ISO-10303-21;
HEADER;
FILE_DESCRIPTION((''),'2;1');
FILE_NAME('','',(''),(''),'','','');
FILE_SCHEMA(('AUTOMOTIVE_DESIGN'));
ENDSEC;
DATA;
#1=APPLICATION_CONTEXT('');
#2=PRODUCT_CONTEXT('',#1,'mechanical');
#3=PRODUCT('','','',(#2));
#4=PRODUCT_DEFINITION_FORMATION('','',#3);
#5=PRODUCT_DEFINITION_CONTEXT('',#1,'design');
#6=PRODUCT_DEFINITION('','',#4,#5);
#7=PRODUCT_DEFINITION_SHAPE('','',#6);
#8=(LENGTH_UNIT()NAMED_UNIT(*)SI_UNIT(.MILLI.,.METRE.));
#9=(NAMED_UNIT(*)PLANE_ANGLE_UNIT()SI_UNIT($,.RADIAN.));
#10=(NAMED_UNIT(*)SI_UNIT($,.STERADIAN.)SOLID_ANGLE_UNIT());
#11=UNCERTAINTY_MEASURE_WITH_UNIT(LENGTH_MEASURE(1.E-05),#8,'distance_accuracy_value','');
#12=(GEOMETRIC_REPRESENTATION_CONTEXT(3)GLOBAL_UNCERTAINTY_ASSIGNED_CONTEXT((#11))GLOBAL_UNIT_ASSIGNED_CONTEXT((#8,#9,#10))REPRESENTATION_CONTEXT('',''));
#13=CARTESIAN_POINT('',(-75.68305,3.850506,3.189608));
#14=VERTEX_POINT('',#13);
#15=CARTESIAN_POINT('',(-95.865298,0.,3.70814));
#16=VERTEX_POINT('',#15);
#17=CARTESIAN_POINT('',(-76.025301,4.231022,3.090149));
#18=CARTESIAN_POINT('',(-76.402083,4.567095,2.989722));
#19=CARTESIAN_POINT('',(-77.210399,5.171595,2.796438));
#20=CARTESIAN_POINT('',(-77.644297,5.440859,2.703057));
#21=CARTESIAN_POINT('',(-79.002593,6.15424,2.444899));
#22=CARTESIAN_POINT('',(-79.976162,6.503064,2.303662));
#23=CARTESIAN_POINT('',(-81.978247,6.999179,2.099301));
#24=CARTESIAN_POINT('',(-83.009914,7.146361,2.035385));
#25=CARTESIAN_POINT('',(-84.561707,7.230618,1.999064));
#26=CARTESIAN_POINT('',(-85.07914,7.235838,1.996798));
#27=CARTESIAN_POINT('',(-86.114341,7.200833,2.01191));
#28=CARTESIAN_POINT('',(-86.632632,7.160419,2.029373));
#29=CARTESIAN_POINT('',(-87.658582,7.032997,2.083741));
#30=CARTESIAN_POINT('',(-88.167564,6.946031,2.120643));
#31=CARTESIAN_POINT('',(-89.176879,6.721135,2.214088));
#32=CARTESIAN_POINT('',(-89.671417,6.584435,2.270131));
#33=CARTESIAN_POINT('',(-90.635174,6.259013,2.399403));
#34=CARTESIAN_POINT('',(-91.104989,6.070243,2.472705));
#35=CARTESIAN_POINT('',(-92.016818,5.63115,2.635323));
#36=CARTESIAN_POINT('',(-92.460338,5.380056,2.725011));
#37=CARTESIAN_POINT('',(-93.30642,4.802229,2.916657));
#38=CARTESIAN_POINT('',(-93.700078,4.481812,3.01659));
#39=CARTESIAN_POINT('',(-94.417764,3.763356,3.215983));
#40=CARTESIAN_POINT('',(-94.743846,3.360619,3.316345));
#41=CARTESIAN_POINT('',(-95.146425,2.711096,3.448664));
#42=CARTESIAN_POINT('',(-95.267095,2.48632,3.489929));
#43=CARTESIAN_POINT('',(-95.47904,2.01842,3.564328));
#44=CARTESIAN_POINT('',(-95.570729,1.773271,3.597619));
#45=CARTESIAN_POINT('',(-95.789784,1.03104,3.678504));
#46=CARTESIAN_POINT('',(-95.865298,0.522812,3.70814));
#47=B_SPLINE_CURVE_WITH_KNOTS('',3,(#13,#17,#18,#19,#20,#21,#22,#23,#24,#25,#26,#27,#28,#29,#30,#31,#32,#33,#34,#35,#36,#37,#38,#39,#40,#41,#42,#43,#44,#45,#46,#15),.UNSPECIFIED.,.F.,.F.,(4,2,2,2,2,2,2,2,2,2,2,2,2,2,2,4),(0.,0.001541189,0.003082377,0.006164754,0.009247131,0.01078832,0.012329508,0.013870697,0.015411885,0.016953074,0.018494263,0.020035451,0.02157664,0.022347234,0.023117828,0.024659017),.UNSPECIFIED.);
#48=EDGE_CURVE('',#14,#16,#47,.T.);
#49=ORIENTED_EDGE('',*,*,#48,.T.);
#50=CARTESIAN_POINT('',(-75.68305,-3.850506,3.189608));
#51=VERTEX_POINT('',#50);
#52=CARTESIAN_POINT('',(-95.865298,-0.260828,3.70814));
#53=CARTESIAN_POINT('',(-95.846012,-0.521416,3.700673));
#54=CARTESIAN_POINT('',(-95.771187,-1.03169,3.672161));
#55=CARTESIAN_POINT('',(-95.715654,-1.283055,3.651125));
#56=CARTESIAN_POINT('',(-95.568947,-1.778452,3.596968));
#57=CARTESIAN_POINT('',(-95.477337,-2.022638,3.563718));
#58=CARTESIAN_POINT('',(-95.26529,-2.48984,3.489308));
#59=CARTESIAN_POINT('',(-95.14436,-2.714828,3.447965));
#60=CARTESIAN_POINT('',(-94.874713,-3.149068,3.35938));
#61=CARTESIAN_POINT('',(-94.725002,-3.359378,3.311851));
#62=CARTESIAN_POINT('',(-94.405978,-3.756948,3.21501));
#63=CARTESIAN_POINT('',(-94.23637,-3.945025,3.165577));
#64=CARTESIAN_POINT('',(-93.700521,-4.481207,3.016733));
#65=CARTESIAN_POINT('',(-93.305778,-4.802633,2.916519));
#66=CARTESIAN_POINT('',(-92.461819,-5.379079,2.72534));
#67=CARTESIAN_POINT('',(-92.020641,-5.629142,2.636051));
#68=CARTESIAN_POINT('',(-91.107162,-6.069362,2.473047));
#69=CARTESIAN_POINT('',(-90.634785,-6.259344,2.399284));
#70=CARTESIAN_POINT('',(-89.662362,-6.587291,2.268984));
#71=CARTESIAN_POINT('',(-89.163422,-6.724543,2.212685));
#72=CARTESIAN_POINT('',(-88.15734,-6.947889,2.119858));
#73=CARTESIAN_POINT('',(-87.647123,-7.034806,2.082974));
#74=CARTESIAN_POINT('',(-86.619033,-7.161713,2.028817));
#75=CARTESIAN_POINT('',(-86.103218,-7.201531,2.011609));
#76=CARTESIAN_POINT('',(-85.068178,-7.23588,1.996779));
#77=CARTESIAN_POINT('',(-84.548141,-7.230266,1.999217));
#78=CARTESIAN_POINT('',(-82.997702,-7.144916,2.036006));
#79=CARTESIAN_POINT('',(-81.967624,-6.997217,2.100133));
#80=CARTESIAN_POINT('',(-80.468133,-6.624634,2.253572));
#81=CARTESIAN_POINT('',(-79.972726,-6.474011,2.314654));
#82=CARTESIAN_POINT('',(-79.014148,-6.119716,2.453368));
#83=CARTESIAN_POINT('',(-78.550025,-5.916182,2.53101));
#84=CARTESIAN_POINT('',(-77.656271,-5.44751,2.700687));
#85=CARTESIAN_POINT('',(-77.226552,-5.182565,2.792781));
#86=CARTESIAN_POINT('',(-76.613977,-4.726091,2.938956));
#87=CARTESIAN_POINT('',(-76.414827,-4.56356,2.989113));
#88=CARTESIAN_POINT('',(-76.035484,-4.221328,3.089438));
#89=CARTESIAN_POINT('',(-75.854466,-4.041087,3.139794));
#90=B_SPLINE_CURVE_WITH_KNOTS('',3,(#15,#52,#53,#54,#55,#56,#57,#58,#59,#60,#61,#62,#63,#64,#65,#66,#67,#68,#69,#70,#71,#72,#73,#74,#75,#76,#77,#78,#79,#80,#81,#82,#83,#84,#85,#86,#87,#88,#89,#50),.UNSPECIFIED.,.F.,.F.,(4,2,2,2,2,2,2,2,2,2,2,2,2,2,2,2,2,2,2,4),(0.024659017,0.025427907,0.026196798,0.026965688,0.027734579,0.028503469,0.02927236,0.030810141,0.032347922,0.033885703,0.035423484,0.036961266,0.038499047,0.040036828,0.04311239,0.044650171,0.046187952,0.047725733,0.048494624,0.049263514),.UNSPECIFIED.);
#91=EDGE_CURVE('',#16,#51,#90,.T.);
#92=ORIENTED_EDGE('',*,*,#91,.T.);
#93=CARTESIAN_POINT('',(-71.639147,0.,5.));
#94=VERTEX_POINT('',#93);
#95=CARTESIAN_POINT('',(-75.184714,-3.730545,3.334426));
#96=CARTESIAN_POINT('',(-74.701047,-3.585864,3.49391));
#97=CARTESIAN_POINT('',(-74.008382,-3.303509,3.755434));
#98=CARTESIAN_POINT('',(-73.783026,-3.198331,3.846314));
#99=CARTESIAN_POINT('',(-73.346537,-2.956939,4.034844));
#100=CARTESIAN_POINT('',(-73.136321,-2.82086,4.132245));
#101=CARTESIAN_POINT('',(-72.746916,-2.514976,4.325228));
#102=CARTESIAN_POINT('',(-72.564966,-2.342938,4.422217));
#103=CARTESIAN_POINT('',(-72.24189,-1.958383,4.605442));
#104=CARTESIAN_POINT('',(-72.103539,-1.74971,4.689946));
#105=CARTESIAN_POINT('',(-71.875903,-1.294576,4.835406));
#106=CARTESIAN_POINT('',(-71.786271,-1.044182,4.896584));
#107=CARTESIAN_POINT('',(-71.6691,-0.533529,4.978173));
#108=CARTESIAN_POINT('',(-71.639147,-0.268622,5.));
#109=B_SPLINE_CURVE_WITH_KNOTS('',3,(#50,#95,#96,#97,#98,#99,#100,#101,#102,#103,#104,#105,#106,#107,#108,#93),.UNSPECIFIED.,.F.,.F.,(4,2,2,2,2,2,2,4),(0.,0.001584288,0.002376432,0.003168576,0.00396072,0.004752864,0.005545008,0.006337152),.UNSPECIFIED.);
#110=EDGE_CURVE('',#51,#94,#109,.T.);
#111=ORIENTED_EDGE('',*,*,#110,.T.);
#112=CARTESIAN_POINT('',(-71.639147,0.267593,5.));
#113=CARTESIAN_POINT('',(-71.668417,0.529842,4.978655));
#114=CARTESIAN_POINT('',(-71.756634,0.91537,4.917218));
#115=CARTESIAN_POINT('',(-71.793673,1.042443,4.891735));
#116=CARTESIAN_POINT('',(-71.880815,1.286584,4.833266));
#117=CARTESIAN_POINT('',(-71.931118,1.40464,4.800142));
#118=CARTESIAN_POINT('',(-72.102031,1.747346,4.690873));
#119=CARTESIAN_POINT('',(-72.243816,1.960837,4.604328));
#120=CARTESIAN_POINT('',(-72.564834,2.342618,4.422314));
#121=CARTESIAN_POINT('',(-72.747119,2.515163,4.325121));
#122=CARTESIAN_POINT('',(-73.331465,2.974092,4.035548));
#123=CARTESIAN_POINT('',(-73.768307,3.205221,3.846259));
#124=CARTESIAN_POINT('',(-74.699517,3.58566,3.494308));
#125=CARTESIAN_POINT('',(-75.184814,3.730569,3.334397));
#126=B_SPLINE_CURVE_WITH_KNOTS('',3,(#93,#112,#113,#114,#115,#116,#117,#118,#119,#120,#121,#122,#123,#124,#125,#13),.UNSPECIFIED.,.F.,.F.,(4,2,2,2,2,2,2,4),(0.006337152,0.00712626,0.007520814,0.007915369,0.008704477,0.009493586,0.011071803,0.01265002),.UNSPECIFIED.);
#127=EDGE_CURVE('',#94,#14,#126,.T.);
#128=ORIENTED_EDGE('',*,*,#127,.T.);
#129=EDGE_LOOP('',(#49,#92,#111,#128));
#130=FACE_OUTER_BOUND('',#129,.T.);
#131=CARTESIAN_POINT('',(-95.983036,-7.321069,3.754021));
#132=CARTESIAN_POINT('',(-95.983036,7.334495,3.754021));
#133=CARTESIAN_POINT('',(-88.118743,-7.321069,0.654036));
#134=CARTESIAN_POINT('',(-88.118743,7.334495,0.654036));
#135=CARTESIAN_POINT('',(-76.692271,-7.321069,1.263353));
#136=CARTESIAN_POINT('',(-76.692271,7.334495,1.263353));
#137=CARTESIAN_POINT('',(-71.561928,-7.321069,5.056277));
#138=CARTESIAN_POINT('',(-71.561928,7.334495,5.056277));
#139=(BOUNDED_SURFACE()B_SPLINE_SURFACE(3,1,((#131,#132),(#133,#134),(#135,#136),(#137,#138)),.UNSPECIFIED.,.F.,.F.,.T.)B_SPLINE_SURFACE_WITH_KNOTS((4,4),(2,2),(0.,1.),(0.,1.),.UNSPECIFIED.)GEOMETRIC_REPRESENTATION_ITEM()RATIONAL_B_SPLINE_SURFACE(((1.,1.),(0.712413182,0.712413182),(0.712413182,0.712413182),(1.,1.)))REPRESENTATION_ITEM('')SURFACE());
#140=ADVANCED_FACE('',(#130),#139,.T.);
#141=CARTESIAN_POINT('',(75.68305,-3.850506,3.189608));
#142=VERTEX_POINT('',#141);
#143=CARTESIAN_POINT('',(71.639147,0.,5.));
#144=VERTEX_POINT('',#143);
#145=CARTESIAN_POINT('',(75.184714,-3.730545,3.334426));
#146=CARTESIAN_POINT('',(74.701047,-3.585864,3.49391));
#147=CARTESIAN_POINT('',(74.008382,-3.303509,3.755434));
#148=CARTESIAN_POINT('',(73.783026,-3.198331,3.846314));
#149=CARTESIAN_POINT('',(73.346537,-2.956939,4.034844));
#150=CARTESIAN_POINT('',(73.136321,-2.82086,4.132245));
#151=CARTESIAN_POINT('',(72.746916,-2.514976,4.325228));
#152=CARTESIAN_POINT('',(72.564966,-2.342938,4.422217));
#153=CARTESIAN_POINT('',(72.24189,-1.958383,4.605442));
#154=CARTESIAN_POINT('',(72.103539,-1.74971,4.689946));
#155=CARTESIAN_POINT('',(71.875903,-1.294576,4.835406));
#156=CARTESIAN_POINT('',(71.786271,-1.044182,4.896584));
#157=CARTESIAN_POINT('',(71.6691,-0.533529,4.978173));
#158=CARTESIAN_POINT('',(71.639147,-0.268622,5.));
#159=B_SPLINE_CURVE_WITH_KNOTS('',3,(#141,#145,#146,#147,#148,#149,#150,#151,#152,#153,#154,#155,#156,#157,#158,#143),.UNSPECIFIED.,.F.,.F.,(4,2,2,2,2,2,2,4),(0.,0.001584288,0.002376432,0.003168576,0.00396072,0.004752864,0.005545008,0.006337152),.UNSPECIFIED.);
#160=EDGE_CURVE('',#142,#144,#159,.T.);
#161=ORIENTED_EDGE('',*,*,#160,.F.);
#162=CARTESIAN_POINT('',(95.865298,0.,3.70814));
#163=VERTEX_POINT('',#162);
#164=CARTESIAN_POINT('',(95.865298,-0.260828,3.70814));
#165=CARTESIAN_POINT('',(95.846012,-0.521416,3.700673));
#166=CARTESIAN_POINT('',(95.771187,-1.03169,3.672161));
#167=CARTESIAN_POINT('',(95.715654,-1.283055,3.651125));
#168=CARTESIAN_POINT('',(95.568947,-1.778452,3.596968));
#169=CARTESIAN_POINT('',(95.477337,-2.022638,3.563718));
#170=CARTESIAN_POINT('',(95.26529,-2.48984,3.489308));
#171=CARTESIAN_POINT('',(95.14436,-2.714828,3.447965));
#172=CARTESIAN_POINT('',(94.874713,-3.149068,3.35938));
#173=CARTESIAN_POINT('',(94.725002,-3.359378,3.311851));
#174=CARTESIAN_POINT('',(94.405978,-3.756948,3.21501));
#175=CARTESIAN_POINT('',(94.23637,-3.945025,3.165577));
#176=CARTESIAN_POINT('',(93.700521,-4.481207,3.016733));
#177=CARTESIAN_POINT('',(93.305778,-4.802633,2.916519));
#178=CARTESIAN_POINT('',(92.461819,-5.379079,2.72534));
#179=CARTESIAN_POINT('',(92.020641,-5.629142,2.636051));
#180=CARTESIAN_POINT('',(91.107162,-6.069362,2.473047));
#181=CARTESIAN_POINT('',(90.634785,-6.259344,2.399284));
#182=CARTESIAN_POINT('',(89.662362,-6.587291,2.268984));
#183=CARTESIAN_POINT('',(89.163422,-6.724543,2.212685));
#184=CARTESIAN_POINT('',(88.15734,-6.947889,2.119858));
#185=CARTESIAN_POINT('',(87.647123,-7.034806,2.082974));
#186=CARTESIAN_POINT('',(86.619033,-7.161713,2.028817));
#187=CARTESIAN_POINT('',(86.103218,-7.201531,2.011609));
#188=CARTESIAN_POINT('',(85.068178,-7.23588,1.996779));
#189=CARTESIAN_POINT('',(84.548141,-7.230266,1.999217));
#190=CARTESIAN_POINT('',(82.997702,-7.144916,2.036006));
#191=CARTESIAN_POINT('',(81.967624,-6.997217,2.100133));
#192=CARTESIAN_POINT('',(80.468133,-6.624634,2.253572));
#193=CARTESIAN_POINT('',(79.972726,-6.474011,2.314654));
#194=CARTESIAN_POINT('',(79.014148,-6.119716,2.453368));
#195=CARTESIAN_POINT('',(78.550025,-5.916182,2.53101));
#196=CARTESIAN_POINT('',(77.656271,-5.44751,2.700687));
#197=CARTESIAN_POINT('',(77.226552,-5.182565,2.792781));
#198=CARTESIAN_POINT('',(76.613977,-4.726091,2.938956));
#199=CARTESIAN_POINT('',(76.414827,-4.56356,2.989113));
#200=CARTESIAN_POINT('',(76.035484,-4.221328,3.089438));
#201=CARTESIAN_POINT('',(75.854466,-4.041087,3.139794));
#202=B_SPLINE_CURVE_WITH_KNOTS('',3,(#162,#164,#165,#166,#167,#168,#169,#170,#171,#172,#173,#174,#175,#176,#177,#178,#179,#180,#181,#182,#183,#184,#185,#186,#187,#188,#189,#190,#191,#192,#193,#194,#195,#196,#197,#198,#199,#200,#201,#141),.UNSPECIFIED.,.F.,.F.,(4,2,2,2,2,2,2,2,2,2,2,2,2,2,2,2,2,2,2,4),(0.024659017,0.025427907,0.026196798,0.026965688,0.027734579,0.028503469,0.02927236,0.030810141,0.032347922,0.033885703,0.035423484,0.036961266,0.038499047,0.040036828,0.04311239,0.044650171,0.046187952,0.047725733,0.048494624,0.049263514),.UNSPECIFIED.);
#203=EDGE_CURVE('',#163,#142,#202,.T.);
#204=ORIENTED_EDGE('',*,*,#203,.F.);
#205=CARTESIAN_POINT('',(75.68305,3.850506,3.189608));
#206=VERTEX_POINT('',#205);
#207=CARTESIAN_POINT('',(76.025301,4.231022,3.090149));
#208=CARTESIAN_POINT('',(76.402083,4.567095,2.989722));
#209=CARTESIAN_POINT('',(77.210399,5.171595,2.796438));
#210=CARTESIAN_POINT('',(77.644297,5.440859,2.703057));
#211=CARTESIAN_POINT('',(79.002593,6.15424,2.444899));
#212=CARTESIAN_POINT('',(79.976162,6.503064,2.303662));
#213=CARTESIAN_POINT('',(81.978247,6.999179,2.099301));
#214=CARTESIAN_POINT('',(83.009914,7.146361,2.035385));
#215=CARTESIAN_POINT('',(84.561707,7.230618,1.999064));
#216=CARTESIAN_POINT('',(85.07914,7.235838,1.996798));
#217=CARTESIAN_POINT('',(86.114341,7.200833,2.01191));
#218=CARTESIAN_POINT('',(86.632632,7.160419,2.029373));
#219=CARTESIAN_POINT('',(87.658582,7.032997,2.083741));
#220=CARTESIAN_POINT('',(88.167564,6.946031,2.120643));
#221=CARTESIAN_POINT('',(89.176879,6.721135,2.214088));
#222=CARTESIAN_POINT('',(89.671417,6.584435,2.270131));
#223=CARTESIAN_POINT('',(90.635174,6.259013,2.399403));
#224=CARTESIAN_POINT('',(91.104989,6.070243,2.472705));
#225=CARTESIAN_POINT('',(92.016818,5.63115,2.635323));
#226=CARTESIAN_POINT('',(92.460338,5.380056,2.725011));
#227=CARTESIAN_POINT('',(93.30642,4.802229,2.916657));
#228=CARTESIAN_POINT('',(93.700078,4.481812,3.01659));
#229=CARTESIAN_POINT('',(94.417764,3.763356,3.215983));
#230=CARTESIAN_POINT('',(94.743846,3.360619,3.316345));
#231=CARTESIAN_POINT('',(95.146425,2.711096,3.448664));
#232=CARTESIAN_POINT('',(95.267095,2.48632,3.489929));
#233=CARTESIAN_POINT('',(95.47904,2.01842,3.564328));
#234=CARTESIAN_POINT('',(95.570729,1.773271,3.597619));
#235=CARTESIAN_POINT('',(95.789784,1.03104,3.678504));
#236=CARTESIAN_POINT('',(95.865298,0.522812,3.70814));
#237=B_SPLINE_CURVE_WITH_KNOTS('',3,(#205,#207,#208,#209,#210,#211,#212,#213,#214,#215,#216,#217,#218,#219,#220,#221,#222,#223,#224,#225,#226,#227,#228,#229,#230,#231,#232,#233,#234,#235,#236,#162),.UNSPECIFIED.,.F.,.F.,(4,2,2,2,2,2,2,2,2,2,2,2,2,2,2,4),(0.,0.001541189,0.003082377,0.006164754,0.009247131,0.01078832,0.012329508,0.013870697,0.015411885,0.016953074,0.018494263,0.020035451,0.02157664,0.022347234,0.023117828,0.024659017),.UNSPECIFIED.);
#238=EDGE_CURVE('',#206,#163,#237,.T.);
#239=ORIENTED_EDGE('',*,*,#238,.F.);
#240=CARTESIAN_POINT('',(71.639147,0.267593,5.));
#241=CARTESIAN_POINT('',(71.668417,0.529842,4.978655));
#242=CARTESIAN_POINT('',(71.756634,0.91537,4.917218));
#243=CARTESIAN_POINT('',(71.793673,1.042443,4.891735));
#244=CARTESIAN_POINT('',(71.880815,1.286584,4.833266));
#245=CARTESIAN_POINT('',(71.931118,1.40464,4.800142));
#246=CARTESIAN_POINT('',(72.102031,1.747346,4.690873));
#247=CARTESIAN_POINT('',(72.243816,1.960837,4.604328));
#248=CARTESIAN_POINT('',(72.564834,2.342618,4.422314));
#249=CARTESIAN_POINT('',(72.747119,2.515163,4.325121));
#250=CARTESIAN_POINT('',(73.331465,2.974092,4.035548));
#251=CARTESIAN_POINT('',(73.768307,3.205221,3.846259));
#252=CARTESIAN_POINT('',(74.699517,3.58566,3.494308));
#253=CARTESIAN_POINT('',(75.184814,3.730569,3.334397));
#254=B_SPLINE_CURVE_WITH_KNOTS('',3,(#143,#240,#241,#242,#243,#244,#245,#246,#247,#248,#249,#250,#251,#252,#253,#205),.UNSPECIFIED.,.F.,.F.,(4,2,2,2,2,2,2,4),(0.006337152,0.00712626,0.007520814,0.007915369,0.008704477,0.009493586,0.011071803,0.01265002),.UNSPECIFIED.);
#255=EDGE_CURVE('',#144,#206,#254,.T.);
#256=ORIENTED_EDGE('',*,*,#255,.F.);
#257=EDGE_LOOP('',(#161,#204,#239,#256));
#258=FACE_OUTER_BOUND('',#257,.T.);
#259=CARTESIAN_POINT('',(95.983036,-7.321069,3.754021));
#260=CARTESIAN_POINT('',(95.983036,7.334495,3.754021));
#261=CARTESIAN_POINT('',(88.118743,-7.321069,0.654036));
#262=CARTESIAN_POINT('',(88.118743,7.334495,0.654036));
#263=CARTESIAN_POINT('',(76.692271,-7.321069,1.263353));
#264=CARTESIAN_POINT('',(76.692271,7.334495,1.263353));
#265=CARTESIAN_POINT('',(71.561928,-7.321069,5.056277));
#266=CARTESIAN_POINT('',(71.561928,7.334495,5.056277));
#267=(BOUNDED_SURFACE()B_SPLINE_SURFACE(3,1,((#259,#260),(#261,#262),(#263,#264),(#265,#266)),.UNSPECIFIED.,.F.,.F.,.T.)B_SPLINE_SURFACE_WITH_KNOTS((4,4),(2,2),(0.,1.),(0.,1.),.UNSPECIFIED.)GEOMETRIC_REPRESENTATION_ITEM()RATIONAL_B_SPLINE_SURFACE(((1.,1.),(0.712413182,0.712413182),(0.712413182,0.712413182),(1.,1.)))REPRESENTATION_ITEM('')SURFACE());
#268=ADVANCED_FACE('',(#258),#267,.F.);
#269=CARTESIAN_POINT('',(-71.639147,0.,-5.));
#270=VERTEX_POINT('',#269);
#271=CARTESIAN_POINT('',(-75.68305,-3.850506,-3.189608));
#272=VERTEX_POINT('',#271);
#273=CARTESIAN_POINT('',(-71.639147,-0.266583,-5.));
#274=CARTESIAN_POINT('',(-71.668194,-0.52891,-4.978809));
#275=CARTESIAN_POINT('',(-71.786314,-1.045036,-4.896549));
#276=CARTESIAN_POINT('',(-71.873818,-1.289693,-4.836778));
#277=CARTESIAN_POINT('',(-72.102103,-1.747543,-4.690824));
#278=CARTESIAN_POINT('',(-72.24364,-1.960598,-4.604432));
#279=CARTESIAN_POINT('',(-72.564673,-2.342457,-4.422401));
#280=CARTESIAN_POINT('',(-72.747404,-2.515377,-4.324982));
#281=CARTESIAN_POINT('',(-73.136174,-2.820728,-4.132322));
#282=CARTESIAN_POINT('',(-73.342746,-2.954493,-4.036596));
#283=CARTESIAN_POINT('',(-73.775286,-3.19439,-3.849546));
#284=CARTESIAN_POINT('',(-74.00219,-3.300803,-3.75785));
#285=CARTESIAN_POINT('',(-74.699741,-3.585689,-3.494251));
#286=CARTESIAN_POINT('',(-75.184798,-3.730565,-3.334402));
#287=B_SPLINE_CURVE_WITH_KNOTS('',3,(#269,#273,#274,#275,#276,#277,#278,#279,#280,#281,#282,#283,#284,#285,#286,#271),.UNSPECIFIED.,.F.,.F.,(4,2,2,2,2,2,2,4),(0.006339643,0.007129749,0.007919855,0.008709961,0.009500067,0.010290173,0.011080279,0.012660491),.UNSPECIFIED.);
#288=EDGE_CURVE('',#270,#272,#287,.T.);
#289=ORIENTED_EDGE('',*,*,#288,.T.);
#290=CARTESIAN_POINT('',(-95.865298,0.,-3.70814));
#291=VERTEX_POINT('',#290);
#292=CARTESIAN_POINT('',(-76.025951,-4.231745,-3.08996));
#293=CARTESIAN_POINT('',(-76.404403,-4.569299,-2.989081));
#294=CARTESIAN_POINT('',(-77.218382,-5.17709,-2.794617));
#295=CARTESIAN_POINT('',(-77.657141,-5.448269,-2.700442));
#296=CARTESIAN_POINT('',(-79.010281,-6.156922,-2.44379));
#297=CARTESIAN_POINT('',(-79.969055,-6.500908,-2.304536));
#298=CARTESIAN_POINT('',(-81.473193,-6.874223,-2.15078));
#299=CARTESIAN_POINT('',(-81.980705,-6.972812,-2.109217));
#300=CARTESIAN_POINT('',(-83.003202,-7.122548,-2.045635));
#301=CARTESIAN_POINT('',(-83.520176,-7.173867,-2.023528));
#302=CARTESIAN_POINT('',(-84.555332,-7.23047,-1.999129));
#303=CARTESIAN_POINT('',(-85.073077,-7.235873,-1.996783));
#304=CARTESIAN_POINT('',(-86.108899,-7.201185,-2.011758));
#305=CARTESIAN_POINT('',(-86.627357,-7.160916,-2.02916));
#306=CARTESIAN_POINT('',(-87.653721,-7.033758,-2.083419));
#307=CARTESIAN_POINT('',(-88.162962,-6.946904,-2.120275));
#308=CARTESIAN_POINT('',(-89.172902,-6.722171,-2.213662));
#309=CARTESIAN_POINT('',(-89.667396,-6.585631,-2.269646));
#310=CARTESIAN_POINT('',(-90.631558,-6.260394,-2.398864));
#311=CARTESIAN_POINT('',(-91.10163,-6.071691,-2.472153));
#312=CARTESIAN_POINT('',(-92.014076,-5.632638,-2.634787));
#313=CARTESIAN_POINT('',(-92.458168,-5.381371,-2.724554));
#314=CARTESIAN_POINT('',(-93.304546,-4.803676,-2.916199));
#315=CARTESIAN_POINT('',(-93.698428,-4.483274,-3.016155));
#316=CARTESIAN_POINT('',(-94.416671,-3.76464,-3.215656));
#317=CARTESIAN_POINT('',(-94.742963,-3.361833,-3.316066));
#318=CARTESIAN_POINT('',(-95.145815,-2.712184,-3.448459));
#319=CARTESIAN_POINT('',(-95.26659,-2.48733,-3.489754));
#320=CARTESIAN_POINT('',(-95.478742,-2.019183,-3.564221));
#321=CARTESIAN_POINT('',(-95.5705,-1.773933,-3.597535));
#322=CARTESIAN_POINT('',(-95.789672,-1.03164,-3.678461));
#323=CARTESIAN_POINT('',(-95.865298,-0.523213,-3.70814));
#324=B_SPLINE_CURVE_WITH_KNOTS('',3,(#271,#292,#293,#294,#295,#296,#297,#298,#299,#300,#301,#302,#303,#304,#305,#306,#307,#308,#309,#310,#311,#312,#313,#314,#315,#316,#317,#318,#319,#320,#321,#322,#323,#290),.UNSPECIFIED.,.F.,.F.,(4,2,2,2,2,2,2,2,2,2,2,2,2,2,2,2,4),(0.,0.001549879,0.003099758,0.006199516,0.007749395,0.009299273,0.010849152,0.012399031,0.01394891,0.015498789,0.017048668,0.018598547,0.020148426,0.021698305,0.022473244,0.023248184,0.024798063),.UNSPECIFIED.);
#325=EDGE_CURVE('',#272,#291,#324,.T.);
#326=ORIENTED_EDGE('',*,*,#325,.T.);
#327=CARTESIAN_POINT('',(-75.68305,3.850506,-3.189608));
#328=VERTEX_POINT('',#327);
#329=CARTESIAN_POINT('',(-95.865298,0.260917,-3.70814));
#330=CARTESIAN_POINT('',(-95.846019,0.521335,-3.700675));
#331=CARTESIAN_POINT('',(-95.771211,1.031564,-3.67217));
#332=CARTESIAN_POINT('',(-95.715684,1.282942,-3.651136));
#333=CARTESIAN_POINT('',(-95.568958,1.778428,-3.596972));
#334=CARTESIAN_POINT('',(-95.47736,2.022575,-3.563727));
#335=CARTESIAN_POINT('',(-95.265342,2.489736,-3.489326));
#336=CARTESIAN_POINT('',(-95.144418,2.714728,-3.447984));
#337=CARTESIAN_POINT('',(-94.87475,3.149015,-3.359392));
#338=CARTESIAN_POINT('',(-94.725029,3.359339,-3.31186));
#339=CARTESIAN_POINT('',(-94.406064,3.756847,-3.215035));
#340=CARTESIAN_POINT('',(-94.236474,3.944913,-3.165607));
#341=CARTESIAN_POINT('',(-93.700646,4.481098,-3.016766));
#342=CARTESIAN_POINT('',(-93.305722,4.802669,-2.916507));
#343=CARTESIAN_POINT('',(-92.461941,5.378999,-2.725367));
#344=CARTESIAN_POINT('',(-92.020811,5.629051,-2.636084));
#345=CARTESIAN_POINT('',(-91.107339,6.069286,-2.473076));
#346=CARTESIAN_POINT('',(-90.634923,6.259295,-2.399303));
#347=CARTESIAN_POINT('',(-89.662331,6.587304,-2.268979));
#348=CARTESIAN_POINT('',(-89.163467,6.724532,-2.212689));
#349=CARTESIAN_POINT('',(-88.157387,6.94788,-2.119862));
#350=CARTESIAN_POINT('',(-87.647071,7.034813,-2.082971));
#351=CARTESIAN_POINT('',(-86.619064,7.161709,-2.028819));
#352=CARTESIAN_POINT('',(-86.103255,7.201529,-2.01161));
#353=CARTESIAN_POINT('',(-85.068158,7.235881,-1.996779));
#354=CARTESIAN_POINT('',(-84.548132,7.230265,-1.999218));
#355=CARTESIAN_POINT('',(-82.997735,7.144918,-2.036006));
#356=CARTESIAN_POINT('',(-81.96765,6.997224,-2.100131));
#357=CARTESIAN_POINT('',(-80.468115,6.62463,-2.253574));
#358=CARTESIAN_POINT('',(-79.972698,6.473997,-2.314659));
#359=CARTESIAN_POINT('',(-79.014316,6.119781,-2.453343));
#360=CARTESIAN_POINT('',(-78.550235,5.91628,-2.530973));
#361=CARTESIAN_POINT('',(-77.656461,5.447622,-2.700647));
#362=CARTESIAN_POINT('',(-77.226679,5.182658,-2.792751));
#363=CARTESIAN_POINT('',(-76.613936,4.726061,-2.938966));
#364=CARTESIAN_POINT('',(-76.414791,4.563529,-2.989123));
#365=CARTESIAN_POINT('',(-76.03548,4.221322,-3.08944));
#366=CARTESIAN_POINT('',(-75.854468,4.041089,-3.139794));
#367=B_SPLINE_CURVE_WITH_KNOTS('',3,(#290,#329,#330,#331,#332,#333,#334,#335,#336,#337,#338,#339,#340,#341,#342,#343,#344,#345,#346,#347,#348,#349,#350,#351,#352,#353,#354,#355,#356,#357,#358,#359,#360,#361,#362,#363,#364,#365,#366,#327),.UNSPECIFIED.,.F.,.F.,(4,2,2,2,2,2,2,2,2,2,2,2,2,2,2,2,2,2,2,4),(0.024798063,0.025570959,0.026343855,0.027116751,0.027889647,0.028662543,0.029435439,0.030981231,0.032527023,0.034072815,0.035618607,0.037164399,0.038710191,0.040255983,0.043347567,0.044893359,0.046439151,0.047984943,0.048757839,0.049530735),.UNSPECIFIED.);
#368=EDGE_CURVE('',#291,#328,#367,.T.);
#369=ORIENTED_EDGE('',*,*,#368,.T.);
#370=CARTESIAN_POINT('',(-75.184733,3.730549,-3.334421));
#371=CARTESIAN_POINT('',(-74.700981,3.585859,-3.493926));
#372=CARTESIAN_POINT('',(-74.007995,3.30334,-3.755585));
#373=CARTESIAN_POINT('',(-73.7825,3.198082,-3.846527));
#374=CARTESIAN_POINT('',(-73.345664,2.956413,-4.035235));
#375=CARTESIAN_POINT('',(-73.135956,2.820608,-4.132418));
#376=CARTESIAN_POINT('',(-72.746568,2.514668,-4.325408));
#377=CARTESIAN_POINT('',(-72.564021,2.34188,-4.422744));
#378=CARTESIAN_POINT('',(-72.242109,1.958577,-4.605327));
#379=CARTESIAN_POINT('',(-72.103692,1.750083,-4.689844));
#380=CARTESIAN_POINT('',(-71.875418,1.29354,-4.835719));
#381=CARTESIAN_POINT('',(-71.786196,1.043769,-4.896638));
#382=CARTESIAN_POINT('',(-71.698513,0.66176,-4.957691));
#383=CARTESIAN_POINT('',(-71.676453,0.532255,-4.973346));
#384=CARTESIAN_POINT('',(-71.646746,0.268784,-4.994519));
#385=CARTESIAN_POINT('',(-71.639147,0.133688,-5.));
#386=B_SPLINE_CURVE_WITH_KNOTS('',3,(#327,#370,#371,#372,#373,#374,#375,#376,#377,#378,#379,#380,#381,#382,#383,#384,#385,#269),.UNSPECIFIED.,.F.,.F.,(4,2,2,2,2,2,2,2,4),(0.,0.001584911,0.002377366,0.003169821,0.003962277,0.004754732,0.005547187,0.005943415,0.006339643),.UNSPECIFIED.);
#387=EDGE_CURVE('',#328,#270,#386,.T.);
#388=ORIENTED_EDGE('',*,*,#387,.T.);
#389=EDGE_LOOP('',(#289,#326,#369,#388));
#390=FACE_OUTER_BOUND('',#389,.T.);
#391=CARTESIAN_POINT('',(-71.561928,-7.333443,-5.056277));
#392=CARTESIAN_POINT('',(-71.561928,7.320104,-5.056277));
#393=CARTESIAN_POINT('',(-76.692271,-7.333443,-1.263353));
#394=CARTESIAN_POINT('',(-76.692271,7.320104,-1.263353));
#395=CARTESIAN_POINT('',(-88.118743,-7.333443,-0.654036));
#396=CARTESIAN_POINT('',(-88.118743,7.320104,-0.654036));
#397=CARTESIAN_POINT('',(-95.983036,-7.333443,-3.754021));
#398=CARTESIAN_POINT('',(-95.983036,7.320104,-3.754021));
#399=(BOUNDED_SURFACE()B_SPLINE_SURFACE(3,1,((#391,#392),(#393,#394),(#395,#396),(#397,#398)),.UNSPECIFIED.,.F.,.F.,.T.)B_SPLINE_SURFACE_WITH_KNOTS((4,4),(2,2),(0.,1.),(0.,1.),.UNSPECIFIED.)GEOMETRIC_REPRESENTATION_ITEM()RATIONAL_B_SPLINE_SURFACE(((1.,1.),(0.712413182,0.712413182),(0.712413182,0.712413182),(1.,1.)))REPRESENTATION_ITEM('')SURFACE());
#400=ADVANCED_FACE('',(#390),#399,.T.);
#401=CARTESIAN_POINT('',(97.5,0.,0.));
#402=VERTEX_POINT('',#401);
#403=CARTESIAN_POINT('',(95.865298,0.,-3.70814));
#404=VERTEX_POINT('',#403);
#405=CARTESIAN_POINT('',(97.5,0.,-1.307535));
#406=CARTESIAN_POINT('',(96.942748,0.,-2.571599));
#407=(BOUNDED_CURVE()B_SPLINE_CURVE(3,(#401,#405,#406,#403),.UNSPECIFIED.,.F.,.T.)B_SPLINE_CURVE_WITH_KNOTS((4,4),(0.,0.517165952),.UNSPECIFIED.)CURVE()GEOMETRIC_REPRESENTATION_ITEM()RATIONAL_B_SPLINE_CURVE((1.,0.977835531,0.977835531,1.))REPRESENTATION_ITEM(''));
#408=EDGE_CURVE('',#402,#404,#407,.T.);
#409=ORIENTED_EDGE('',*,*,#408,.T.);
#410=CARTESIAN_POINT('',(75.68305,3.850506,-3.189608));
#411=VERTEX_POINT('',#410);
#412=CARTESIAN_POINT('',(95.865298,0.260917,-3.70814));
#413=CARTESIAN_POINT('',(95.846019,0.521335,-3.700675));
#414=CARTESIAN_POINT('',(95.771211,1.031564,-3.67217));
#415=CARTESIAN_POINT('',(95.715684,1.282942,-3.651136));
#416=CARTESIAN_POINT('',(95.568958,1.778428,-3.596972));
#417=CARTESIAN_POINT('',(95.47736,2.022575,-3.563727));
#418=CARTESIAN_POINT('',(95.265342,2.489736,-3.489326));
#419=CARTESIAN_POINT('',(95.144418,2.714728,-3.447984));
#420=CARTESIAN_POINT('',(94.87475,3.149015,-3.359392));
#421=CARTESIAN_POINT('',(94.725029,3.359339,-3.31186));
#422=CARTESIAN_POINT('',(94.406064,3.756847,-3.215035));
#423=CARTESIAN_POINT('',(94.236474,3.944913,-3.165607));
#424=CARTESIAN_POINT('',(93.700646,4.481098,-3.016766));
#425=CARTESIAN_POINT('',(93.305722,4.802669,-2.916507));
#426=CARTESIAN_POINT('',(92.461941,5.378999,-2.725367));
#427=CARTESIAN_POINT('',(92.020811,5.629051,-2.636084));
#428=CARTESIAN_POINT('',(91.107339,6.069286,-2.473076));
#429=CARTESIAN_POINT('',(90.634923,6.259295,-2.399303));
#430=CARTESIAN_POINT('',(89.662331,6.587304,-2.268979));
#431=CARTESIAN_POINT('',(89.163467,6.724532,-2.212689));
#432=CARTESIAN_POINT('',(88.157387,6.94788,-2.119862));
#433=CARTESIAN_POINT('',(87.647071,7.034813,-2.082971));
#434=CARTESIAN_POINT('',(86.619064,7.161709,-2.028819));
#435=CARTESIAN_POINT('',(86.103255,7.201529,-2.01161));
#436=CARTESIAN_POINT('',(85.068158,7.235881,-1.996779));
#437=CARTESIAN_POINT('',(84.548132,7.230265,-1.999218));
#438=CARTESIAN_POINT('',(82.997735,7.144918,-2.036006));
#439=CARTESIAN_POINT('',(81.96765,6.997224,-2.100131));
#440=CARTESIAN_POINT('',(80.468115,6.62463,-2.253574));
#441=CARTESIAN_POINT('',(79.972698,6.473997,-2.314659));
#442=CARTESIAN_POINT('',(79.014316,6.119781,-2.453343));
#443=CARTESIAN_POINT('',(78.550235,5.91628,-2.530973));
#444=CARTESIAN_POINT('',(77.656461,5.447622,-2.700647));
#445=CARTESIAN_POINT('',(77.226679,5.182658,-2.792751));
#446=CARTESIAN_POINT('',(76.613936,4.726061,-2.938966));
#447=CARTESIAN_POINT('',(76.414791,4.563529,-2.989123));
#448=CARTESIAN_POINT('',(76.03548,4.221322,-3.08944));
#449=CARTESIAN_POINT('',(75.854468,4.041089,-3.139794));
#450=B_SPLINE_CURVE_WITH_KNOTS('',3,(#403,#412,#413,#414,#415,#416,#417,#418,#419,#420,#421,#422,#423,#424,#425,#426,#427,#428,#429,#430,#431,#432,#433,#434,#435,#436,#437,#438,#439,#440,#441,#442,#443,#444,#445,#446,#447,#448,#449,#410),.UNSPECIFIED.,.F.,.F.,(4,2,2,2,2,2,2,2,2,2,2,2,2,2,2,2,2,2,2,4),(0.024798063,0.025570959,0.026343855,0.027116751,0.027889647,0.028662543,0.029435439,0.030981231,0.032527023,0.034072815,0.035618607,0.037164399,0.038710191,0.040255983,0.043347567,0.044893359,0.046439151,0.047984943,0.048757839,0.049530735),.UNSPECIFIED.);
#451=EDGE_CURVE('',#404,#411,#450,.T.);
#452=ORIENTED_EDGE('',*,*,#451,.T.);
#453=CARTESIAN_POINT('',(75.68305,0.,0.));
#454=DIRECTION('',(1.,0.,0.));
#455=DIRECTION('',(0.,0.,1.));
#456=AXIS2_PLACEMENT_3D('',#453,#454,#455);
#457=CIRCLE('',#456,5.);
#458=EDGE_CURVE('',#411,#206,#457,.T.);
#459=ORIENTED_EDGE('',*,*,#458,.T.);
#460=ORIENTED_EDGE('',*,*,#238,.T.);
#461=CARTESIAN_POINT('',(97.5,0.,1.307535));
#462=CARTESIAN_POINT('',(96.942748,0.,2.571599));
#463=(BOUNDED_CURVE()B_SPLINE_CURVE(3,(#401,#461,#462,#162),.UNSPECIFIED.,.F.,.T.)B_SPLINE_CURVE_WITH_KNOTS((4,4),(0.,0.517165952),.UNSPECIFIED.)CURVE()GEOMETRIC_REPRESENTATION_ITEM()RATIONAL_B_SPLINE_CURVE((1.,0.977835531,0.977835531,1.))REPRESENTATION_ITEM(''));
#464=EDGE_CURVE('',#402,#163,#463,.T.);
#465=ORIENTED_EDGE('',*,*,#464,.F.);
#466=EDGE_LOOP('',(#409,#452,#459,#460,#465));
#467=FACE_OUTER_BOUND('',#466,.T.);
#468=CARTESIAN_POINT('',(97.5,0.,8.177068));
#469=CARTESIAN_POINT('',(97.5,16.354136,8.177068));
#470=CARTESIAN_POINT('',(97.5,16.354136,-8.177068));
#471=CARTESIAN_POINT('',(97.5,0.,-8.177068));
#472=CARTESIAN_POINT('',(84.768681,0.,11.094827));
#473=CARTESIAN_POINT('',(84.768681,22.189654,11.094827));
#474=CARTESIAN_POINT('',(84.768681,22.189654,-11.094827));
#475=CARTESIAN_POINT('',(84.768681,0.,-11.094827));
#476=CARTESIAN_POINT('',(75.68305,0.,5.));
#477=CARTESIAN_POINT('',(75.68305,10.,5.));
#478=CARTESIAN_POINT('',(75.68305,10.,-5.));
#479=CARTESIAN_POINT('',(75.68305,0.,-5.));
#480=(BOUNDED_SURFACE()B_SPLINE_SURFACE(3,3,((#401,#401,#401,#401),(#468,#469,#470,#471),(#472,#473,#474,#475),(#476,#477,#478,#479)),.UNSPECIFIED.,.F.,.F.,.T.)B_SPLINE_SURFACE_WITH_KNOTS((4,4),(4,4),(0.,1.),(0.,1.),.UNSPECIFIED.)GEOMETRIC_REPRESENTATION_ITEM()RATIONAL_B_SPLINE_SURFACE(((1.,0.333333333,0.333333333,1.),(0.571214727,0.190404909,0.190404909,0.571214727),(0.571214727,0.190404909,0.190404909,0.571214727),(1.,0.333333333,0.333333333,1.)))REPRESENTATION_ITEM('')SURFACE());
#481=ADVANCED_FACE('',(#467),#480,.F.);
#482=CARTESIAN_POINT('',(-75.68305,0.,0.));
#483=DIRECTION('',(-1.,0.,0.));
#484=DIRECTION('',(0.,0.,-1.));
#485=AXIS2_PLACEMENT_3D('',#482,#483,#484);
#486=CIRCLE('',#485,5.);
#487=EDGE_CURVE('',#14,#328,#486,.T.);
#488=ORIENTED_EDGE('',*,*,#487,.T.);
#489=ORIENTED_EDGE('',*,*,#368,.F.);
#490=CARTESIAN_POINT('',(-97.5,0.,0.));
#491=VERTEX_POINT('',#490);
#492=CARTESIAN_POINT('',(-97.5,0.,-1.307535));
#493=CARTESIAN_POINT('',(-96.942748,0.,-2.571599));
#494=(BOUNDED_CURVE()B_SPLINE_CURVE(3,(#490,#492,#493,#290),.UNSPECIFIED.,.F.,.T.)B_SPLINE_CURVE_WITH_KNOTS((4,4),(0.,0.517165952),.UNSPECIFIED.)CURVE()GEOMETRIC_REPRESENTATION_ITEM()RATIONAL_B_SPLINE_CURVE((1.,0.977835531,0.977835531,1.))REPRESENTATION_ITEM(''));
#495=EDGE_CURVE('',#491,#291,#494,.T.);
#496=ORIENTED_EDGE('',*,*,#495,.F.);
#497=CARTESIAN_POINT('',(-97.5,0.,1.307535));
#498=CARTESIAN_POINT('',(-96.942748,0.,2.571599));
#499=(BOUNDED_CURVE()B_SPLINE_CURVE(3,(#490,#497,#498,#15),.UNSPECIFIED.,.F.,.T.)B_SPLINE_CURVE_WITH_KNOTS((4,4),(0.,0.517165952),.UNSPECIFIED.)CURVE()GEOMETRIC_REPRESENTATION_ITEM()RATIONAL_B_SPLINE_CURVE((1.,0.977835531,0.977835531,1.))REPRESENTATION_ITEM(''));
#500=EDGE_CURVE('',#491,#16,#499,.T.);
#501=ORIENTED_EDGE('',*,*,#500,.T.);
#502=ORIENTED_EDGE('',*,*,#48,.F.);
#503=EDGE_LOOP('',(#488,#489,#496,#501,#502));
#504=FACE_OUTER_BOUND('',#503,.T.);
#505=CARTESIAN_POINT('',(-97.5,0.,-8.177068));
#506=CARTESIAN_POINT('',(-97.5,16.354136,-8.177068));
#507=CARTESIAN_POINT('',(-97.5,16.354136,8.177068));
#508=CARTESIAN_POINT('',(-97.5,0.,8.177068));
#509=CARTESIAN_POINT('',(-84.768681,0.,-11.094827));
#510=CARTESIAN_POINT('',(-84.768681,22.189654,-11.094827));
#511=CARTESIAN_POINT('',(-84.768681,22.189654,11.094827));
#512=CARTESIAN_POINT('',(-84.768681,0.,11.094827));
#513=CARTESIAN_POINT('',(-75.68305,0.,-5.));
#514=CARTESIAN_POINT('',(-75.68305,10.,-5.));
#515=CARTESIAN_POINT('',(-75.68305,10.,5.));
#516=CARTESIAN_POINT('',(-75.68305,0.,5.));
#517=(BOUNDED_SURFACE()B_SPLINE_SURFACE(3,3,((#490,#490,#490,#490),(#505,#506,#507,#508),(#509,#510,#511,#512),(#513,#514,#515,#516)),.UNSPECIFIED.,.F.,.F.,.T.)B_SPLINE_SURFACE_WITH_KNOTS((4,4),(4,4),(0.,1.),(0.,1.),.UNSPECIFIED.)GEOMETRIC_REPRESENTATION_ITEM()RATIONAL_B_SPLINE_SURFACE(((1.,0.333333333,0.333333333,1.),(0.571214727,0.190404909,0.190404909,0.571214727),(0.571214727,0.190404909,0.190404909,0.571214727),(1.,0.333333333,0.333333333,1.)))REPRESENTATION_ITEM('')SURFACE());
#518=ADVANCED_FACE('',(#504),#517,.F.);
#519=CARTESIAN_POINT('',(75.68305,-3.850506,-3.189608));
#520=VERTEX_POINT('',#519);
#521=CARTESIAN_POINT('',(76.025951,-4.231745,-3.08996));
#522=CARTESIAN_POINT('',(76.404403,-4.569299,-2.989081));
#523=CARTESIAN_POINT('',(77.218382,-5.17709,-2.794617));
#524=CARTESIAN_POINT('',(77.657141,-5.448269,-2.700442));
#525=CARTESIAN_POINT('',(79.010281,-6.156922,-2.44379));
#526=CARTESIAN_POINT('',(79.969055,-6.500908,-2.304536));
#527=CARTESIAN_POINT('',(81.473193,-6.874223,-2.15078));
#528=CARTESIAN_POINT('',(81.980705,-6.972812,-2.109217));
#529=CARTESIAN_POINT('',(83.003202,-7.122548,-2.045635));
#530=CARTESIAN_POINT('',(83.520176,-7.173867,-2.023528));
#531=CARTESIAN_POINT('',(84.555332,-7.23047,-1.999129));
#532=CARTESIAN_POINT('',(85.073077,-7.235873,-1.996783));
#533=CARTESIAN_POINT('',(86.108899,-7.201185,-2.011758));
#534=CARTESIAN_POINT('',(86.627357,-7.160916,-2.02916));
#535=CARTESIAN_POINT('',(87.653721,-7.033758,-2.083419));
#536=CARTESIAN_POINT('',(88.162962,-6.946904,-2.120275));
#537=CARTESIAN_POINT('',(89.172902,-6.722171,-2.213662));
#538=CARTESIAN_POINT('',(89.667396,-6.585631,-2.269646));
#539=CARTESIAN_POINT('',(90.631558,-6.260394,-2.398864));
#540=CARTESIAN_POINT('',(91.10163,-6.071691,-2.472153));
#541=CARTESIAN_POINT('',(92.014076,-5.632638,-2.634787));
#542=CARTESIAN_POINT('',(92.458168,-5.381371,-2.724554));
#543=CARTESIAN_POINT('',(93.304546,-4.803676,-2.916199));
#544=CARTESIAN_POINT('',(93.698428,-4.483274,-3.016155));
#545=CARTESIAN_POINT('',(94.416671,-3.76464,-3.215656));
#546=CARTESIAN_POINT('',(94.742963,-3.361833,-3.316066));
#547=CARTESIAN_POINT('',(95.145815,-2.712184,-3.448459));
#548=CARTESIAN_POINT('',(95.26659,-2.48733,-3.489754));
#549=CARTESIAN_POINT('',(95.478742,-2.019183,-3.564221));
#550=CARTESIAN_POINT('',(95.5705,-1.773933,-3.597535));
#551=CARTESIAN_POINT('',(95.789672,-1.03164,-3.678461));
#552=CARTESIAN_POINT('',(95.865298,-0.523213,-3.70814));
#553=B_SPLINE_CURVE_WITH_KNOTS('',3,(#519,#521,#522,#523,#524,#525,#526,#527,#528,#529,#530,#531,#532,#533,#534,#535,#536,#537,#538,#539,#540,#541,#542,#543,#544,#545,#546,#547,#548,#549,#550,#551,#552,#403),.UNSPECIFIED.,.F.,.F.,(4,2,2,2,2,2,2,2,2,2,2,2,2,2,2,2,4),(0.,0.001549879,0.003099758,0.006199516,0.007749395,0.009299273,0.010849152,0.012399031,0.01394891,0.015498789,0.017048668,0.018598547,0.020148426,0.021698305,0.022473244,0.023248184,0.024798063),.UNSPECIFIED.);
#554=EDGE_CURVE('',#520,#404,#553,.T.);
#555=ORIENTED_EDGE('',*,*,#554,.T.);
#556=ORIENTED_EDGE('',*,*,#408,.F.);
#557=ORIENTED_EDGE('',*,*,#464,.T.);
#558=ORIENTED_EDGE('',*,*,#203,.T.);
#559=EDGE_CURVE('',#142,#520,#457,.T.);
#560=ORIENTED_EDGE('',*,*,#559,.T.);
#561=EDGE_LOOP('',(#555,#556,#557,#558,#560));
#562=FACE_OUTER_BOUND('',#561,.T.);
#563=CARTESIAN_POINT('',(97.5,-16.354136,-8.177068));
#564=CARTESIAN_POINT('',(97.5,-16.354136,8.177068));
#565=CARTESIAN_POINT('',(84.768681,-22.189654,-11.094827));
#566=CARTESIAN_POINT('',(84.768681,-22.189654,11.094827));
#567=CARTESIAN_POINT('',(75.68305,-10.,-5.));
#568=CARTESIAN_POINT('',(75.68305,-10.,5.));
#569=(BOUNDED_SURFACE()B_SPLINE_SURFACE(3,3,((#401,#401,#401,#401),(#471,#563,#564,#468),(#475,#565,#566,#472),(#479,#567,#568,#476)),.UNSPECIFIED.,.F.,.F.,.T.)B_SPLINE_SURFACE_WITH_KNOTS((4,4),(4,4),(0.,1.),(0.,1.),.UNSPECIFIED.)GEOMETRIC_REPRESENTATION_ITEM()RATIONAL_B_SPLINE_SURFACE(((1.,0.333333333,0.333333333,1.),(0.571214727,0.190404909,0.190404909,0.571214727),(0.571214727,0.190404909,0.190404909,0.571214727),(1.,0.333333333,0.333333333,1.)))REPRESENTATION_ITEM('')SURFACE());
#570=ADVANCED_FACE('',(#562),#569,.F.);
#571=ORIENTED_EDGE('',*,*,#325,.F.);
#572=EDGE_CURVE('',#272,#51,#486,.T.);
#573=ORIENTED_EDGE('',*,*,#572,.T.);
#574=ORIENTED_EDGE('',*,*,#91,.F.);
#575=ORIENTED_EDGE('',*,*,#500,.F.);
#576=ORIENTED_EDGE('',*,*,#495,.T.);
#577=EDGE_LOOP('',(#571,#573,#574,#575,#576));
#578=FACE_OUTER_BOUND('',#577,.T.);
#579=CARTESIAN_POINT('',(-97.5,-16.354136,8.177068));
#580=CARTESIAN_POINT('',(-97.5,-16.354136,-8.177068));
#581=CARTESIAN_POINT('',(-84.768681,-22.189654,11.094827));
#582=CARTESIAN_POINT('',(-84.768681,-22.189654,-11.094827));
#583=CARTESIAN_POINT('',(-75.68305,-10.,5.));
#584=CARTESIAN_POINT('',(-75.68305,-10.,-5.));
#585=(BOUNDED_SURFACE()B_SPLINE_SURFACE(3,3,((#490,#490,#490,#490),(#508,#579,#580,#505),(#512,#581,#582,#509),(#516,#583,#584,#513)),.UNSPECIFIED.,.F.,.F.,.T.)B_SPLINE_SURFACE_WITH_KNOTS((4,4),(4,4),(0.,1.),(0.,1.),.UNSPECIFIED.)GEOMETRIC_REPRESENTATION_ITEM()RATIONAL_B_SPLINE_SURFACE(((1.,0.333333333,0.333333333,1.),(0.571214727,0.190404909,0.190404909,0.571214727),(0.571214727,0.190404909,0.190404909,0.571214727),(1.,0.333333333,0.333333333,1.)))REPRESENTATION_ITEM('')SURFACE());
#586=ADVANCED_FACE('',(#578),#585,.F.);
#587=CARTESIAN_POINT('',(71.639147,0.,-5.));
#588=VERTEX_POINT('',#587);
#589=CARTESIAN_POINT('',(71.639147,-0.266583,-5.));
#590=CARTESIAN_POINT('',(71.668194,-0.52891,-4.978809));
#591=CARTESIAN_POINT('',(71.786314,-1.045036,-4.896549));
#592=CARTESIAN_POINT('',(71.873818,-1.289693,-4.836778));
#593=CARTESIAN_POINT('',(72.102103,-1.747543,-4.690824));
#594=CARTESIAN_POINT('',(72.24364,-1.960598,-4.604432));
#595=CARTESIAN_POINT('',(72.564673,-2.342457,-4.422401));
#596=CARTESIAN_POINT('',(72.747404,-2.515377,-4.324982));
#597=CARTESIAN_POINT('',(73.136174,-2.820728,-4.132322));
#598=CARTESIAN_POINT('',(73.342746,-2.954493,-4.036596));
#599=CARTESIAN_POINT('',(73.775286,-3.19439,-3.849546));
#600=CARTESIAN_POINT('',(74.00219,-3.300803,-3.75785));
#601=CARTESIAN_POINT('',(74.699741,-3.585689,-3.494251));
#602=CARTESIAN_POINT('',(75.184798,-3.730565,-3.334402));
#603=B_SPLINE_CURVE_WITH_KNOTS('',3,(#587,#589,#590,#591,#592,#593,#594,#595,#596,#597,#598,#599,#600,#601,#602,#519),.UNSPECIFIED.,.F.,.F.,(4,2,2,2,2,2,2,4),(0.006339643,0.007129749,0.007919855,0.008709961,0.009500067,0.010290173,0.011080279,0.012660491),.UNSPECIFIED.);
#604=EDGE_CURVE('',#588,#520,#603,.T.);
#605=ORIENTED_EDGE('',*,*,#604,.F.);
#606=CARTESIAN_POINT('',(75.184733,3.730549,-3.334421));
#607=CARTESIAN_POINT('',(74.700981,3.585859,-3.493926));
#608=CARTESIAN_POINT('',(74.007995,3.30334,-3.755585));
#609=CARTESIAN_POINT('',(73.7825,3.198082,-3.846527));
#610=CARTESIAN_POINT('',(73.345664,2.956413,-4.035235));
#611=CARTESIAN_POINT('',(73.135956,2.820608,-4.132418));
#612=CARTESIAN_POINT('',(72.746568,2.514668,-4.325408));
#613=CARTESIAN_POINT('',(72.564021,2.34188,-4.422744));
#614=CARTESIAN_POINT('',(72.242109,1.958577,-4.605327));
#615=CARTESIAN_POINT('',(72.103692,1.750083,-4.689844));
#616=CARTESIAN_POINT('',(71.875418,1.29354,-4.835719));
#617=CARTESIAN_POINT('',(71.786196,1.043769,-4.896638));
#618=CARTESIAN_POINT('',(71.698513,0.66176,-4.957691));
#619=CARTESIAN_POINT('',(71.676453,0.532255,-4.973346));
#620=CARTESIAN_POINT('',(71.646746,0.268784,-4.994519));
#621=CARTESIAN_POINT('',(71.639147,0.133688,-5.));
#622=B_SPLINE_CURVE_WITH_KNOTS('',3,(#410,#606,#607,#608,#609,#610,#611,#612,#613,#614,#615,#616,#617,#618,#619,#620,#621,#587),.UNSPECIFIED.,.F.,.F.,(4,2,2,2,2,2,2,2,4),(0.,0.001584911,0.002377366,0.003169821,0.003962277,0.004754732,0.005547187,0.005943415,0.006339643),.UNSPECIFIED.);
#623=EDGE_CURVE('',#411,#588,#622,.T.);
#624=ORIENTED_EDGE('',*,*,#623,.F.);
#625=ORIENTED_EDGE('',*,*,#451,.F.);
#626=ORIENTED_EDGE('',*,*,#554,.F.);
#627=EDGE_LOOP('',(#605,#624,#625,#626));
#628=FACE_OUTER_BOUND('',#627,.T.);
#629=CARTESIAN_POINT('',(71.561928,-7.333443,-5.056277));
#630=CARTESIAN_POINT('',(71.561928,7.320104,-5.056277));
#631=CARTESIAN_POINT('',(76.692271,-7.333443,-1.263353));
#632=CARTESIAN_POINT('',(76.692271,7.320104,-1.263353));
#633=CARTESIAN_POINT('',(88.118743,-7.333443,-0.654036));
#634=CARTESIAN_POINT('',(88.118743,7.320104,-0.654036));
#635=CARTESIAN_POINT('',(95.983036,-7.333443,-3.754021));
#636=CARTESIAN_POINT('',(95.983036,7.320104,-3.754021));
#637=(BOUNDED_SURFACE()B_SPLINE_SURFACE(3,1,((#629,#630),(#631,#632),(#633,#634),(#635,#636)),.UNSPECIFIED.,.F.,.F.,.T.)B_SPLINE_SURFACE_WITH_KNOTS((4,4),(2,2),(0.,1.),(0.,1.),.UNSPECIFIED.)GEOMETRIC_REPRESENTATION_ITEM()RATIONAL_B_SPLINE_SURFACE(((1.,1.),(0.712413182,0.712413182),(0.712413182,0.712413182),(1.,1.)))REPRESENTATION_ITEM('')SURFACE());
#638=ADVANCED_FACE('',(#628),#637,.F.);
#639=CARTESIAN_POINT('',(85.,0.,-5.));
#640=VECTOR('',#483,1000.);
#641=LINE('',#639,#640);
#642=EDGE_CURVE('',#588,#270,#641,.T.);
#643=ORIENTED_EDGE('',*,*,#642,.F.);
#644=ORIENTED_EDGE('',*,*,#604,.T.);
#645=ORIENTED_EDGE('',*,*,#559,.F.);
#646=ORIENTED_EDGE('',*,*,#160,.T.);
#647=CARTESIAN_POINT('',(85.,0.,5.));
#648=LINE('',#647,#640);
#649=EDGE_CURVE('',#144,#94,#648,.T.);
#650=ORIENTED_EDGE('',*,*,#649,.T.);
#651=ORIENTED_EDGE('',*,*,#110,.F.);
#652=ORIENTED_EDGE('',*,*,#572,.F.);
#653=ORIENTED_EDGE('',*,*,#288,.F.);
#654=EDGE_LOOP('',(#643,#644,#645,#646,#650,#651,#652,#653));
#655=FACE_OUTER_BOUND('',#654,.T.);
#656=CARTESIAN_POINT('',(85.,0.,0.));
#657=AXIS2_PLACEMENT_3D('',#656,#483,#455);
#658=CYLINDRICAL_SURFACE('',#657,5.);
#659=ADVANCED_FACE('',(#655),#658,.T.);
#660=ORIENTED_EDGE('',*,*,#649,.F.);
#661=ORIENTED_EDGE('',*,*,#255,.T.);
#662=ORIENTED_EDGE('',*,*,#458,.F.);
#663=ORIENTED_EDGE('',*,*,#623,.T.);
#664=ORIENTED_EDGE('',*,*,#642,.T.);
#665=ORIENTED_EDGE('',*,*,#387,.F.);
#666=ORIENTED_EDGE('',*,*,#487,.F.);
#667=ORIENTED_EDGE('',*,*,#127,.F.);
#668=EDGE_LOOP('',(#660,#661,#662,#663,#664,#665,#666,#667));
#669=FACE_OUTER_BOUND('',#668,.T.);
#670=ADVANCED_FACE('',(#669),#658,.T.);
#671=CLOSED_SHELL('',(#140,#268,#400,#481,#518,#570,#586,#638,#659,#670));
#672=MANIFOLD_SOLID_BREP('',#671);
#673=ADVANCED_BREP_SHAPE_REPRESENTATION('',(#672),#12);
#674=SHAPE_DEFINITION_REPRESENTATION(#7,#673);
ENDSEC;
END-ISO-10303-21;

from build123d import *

# Parameters (mm, degrees)
SKETCH1_R           = 5
BOSS_EXTRUDE1_DEPTH = 85
SKETCH4_RX          = 15
SKETCH4_RY          = 5.5
CUT_EXTRUDE1_DEPTH  = 85


with BuildPart() as part:
    # Sketch1 → Boss-Extrude1 (new, symmetric)
    with BuildSketch(Plane(origin=(0, 0, 0), x_dir=(0, 0, -1), z_dir=(1, 0, 0))):
        Circle(SKETCH1_R)
    extrude(amount=BOSS_EXTRUDE1_DEPTH, both=True)

    # Sketch3 → Revolve3 (revolve)
    with BuildSketch(Plane(origin=(0, 0, 0), x_dir=(1, 0, 0), z_dir=(0, 1, 0))):
        with BuildLine():
            Line((97.5, 0), (72.5, 0))
            add(Edge.make_bspline(
                [(97.5, 0), (97.5, 7.5), (85, 7.5), (72.5, 7.5), (72.5, 0)],
                knots=[0, 0, 0, 1.570796327, 1.570796327, 3.141592654, 3.141592654, 3.141592654], degree=2, weights=[1, 0.707106781, 1, 0.707106781, 1]))
        make_face()
    revolve3 = revolve(axis=Axis((85, 0, 0), (1, 0, 0)))

    # Sketch4 → Cut-Extrude1 (cut, symmetric)
    with BuildSketch(Plane(origin=(0, 0, 0), x_dir=(1, 0, 0), z_dir=(0, 1, 0))):
        with Locations((85, 7.5)):
            Ellipse(SKETCH4_RX, SKETCH4_RY)
        with Locations((85, -7.5)):
            Ellipse(SKETCH4_RX, SKETCH4_RY)
    cut_extrude1 = extrude(amount=CUT_EXTRUDE1_DEPTH, both=True, mode=Mode.SUBTRACT)

    # Mirror1: Revolve3, Cut-Extrude1 across plane
    add(revolve3.mirror(Plane(origin=(0, 0, 0), x_dir=(0, 0, 1), z_dir=(1, 0, 0))))
    add(cut_extrude1.mirror(Plane(origin=(0, 0, 0), x_dir=(0, 0, 1), z_dir=(1, 0, 0))), mode=Mode.SUBTRACT)


solid = part.part
